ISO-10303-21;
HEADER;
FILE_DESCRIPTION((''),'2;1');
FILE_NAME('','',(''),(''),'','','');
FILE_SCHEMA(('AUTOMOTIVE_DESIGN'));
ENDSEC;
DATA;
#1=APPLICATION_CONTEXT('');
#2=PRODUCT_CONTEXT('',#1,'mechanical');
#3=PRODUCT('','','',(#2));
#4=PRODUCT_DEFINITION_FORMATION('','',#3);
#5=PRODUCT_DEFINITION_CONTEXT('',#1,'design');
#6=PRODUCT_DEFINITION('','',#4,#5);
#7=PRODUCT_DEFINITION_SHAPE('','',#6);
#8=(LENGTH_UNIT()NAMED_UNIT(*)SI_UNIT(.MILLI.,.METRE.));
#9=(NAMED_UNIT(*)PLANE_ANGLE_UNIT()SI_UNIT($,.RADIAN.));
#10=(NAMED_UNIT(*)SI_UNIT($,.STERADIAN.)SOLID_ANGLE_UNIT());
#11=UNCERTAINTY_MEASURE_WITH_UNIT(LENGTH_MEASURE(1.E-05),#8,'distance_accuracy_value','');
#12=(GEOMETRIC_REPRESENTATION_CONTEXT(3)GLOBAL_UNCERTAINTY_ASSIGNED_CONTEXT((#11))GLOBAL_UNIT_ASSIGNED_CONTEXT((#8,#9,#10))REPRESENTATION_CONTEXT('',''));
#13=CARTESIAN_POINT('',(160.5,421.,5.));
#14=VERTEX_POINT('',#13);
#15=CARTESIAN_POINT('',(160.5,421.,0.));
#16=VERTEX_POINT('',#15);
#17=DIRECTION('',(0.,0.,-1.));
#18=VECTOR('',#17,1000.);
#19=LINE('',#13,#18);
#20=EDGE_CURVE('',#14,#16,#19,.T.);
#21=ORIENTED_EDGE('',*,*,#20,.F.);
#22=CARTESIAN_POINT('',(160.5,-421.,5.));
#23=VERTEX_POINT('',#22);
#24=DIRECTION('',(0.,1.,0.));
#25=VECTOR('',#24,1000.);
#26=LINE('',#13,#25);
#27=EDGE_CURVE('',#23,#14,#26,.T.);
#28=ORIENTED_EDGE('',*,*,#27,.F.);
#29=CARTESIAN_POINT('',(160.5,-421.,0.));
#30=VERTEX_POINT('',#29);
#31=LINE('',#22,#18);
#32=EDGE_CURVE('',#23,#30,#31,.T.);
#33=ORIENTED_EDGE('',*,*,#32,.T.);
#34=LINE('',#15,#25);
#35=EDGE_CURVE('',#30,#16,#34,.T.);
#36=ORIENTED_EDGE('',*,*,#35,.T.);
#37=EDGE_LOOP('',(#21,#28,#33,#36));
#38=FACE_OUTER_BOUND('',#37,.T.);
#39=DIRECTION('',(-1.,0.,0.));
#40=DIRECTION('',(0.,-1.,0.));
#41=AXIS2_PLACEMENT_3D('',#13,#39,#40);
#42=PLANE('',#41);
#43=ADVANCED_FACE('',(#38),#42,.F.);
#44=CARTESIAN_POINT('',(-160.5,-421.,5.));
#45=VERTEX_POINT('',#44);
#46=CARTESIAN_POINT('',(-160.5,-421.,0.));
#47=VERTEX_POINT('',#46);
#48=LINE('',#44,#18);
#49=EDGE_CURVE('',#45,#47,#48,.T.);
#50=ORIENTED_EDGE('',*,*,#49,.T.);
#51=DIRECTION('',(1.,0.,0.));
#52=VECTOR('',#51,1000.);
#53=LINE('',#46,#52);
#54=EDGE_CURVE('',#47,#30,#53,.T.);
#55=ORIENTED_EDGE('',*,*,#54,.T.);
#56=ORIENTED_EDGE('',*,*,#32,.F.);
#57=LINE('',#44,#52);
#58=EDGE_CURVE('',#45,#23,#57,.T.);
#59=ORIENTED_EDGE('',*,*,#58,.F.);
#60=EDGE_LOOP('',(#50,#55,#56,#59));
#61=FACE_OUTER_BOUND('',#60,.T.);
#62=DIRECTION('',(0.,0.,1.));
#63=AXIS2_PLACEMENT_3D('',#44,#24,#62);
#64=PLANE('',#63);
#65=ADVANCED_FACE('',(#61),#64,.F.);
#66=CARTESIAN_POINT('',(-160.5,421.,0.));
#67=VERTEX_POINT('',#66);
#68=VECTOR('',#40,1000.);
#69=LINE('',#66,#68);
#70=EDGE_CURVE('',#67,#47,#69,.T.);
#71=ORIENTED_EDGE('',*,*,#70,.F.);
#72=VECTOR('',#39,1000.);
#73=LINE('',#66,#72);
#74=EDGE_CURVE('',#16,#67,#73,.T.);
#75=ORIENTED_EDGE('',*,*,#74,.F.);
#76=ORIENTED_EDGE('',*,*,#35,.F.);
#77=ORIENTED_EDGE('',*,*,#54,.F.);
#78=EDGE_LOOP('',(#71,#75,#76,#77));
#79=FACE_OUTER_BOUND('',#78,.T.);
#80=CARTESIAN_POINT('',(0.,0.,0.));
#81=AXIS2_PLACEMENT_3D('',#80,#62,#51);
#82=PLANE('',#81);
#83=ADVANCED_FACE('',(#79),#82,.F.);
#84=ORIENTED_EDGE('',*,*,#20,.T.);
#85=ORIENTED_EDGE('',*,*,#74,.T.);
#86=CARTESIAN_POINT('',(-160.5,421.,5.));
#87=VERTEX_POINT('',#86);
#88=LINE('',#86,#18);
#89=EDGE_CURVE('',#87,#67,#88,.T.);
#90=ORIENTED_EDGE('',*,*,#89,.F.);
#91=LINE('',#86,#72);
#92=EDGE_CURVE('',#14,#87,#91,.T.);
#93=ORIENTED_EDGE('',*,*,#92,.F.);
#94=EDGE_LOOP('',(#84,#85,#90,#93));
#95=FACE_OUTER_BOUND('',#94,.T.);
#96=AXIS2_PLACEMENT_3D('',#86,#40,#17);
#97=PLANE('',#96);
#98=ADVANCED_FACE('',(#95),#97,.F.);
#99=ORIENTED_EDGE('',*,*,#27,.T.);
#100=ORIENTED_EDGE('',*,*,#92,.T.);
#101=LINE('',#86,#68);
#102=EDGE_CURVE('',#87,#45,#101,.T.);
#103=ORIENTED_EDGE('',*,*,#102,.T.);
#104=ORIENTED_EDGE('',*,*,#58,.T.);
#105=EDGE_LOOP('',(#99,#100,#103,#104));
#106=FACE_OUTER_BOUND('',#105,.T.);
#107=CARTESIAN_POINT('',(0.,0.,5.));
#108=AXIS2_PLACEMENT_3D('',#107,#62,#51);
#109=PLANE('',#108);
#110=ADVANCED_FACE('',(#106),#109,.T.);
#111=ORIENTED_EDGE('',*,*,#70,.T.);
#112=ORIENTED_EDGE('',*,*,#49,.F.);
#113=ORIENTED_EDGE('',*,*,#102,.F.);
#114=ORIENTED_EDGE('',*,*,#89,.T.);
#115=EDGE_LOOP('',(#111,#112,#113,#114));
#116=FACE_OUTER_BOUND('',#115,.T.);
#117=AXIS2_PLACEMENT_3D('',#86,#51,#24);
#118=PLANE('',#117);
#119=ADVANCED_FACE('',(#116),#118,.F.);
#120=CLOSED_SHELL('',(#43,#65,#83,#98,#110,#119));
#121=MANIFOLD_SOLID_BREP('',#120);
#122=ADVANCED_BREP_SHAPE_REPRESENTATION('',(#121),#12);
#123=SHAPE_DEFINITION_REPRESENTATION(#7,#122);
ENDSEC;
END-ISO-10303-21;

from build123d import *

# Parameters (mm, degrees)
SKETCH_1_W      = 321
SKETCH_1_H      = 842
EXTRUDE_1_DEPTH = 5


with BuildPart() as part:
    # 草图1 → 凸台-拉伸1 (new body)
    with BuildSketch(Plane.XY):
        Rectangle(SKETCH_1_W, SKETCH_1_H)
    extrude(amount=EXTRUDE_1_DEPTH)


solid = part.part
